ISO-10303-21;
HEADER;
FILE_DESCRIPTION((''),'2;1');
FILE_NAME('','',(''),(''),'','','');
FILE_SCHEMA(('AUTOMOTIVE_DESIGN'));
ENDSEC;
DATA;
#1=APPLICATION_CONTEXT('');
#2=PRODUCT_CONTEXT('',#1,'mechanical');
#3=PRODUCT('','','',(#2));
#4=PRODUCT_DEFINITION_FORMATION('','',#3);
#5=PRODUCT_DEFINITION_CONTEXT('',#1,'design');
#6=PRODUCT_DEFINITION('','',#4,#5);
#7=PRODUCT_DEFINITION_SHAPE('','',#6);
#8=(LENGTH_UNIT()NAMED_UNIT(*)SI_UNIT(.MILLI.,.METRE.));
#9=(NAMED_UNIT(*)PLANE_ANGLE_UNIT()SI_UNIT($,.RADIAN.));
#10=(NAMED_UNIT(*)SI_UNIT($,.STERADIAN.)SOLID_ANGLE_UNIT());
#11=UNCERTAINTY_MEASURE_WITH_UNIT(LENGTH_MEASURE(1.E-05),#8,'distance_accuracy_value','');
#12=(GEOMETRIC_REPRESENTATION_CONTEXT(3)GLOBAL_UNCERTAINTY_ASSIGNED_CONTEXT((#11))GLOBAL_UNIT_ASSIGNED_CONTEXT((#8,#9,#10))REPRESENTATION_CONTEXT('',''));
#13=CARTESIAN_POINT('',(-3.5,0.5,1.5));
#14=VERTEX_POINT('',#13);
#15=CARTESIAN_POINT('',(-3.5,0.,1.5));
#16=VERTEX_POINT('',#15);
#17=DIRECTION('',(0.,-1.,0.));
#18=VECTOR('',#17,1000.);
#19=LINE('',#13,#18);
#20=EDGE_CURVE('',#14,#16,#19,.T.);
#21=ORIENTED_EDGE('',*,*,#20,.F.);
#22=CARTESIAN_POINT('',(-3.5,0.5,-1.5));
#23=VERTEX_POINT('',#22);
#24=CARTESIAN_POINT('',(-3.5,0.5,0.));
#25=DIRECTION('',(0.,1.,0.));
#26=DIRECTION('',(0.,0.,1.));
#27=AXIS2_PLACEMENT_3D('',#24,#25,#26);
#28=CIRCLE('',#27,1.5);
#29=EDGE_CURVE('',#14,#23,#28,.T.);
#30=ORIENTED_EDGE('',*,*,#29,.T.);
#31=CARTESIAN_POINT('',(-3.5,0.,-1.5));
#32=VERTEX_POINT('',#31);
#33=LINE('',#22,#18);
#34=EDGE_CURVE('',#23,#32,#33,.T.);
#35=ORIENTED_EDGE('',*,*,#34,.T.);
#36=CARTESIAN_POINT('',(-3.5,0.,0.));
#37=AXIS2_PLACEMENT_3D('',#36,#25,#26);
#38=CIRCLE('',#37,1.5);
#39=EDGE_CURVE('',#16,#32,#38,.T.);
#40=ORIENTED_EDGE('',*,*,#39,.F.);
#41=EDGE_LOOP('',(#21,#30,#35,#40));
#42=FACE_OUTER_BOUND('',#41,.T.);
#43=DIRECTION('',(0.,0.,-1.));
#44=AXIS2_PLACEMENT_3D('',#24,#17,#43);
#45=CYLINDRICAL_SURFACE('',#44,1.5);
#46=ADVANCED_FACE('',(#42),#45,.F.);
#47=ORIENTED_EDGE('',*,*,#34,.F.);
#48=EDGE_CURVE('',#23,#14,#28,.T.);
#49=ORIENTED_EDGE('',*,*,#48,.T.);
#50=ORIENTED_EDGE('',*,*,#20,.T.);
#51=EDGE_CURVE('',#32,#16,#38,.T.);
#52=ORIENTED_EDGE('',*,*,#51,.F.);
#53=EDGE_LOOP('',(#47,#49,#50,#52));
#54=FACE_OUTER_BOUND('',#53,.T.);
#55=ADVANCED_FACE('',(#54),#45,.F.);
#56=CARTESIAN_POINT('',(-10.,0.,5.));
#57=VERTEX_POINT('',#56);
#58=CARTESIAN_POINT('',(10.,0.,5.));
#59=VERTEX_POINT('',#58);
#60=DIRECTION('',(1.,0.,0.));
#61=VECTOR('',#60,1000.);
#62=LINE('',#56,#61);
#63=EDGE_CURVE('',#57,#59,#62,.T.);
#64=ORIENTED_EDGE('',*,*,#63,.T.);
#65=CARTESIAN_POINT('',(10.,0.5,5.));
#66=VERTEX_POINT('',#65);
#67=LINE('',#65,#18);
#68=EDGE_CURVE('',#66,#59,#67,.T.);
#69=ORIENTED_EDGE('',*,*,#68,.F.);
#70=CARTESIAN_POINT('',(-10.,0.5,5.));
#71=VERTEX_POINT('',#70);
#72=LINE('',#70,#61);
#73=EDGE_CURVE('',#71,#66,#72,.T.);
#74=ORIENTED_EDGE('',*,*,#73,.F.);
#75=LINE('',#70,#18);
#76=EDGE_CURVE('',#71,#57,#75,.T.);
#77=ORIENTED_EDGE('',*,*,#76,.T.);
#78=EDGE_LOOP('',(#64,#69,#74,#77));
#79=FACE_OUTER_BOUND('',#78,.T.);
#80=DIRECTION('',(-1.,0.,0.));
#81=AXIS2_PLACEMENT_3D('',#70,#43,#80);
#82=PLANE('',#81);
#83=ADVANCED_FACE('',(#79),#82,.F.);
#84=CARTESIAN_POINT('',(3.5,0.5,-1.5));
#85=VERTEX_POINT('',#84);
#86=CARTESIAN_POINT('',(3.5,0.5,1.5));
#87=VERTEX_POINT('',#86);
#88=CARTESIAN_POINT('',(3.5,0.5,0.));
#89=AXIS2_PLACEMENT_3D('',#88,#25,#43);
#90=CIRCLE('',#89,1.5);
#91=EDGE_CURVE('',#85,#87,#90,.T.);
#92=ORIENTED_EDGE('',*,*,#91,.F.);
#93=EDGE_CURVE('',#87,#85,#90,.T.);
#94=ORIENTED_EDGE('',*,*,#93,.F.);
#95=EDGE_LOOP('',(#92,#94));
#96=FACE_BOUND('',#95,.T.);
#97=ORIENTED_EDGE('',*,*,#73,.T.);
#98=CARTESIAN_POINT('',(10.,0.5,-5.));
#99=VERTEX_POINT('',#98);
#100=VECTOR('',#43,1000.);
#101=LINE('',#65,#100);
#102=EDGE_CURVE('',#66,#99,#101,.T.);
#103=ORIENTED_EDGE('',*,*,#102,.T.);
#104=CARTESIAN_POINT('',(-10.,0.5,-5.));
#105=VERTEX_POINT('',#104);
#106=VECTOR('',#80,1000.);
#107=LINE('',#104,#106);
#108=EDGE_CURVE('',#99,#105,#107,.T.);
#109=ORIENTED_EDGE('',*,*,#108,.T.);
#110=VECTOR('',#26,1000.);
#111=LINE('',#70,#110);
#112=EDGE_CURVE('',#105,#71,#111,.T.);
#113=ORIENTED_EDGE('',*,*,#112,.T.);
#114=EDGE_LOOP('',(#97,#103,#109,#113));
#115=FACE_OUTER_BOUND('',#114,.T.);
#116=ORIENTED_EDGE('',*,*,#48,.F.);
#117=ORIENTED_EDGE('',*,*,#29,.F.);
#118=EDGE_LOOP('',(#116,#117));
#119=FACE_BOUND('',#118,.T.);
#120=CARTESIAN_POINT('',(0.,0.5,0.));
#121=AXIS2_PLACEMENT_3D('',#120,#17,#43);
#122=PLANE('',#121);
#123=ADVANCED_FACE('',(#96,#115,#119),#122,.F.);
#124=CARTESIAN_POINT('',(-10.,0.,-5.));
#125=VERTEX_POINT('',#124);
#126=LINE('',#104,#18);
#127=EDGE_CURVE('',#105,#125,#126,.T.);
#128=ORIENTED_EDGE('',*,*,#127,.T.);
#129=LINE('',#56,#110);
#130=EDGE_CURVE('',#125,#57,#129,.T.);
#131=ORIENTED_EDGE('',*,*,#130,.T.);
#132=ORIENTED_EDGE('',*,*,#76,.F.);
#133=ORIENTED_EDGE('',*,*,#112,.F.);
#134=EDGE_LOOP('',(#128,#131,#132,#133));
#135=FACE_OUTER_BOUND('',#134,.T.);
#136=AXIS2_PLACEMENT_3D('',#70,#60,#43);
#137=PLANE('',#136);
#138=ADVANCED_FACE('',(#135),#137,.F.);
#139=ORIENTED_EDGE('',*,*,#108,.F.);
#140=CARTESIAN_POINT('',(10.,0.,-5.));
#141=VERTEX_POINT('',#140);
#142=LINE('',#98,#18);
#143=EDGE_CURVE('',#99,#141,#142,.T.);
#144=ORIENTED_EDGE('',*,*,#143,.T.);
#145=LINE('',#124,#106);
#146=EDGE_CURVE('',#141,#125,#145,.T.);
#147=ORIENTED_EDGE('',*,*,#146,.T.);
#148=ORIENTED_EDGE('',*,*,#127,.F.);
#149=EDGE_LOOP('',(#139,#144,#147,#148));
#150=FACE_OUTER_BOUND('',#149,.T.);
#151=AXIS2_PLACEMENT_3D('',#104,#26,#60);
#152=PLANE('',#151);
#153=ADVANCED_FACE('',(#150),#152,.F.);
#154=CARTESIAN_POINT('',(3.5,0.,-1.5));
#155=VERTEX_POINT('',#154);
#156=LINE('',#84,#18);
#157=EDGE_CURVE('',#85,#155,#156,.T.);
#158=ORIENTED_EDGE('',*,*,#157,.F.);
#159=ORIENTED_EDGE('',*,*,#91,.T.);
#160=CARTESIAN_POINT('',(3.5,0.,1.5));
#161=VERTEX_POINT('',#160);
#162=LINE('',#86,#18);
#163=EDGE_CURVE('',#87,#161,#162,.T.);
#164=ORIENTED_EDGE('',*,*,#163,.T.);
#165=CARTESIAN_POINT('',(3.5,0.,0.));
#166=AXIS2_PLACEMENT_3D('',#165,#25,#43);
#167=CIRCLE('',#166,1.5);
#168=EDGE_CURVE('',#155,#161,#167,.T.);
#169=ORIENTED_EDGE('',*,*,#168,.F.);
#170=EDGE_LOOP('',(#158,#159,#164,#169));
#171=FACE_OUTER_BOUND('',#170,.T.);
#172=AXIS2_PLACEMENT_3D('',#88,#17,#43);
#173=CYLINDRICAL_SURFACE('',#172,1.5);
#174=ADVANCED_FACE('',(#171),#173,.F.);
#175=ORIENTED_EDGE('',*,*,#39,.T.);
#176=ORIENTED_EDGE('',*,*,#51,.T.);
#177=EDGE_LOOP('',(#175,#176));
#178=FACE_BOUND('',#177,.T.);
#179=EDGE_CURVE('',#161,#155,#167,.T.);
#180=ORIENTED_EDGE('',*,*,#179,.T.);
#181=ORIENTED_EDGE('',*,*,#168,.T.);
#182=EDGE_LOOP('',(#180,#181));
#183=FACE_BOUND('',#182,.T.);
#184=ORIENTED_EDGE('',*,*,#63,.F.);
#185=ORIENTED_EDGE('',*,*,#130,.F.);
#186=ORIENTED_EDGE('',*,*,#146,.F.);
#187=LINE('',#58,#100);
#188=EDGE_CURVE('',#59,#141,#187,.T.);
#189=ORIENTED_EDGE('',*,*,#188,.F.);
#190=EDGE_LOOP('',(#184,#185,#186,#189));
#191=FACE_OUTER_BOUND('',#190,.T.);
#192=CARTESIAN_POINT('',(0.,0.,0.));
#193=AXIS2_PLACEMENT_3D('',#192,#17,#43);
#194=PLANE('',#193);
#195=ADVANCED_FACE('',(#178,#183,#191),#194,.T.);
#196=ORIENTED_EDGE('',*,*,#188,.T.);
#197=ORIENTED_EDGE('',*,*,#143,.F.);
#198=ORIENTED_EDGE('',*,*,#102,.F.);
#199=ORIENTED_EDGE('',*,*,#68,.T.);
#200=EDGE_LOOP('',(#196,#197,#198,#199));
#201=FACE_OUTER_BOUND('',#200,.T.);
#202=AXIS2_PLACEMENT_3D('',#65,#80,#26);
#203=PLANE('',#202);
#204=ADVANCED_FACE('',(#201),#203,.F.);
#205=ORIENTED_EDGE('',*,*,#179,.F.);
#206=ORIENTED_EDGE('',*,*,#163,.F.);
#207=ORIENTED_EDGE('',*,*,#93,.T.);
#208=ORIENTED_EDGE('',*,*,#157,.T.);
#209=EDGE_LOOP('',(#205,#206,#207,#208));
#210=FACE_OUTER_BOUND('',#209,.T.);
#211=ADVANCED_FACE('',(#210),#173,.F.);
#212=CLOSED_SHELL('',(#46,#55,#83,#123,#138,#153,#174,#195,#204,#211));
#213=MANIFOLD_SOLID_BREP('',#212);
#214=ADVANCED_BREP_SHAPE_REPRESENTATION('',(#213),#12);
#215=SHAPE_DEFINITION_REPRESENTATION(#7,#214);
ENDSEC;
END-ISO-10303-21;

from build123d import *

# Parameters (mm, degrees)
SKETCH1_W           = 20
SKETCH1_H           = 10
SKETCH1_R           = 1.5
BOSS_EXTRUDE1_DEPTH = 0.5


with BuildPart() as part:
    # Sketch1 → Boss-Extrude1 (new body)
    with BuildSketch(Plane(origin=(0, 0, 0), x_dir=(1, 0, 0), z_dir=(0, 1, 0))):
        Rectangle(SKETCH1_W, SKETCH1_H)
        with Locations(Location((-3.5, 0, 0), (0, 0, 270))):
            Circle(SKETCH1_R, mode=Mode.SUBTRACT)
        with Locations(Location((3.5, 0, 0), (0, 0, 90))):
            Circle(SKETCH1_R, mode=Mode.SUBTRACT)
    extrude(amount=BOSS_EXTRUDE1_DEPTH)


solid = part.part
